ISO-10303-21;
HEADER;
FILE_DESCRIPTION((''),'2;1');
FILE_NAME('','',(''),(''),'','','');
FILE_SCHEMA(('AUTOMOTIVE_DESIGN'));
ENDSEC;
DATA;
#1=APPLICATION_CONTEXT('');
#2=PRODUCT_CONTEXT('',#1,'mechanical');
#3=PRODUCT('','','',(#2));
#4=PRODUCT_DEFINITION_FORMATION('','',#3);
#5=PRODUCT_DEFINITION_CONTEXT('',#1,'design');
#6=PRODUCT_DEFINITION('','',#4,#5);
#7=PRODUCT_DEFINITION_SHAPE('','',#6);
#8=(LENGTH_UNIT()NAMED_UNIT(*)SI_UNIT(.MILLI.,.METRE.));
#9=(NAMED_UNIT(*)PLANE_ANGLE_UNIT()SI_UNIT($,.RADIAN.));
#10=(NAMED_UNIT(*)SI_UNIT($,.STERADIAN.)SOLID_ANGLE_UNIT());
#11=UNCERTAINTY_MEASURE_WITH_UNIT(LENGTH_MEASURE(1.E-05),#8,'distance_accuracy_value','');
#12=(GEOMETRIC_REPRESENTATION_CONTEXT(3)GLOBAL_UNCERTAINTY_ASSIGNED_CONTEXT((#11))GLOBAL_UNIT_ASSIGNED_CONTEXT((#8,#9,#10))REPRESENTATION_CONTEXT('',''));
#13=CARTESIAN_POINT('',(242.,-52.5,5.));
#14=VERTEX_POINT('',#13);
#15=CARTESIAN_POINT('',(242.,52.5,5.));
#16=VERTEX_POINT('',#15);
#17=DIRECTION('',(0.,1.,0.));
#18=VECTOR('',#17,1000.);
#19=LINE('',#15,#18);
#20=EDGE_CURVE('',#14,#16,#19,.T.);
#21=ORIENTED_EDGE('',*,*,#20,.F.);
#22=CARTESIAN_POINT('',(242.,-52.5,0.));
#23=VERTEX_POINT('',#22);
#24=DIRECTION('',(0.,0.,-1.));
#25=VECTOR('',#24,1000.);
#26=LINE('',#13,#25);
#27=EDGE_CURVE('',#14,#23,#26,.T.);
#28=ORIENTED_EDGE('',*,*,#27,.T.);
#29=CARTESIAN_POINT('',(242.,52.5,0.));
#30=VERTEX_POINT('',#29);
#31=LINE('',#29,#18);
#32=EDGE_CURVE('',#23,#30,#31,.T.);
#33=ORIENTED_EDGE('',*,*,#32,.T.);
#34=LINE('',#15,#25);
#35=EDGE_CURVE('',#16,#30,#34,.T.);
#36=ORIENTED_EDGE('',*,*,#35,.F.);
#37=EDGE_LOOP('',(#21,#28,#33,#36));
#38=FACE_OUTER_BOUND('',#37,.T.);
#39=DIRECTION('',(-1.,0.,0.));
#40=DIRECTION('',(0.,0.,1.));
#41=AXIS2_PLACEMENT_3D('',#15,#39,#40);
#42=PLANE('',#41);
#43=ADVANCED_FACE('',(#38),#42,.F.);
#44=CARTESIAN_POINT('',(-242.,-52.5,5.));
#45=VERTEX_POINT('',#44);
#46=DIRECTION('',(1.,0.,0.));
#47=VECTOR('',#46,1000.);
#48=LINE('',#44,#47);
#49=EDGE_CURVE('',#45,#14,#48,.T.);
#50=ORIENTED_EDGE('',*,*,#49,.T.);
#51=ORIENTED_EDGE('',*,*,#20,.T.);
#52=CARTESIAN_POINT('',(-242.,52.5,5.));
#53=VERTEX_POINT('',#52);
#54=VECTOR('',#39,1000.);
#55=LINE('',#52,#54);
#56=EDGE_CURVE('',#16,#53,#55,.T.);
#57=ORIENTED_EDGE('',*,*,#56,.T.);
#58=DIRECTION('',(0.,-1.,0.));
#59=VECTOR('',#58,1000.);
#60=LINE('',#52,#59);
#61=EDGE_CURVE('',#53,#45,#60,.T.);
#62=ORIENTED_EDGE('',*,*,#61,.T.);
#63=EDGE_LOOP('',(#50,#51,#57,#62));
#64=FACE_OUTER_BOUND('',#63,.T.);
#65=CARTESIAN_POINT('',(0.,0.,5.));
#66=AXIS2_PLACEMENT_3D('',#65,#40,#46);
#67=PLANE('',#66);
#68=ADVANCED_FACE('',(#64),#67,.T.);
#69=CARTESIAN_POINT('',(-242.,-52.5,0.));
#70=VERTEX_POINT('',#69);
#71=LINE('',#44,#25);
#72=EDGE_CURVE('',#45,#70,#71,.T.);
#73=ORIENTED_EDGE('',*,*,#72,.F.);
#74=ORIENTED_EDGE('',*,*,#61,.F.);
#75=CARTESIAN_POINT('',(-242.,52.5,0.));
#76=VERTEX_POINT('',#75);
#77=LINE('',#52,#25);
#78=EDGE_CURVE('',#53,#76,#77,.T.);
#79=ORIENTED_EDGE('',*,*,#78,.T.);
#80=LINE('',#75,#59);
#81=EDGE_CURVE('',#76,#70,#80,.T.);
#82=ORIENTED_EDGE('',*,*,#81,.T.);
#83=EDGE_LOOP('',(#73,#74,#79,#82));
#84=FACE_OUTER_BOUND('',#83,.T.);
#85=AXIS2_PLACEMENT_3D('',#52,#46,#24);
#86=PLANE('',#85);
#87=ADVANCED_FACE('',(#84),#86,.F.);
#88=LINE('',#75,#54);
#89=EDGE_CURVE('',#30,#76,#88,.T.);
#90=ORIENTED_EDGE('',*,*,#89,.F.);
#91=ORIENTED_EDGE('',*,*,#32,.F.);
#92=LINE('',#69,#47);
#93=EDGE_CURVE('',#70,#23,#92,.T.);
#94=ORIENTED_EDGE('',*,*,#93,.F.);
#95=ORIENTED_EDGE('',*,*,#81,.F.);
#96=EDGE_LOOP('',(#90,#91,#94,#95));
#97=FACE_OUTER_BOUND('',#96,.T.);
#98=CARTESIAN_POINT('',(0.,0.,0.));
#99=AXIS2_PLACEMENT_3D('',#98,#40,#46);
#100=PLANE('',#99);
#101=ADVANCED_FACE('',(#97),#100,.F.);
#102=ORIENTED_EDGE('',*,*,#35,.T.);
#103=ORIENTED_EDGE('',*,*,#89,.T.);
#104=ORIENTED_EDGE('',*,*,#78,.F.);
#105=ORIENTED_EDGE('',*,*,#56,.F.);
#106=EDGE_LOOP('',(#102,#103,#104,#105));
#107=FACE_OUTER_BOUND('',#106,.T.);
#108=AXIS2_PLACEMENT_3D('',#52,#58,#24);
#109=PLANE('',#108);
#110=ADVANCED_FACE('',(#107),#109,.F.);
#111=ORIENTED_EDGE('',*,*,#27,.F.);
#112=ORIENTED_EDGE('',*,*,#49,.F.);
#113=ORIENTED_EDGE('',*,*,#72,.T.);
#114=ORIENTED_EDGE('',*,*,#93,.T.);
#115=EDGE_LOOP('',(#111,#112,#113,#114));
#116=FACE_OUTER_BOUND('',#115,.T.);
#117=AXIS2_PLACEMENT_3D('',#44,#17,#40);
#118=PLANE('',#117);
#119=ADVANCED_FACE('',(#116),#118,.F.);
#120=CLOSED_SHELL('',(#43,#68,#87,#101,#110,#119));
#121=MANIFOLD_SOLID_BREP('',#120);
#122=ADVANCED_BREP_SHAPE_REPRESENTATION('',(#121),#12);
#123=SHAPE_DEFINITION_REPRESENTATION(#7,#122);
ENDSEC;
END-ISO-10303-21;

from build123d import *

# Parameters (mm, degrees)
SKETCH_1_W      = 484
SKETCH_1_H      = 105
EXTRUDE_1_DEPTH = 5


with BuildPart() as part:
    # 草图1 → 凸台-拉伸1 (new body)
    with BuildSketch(Plane.XY):
        Rectangle(SKETCH_1_W, SKETCH_1_H)
    extrude(amount=EXTRUDE_1_DEPTH)


solid = part.part
